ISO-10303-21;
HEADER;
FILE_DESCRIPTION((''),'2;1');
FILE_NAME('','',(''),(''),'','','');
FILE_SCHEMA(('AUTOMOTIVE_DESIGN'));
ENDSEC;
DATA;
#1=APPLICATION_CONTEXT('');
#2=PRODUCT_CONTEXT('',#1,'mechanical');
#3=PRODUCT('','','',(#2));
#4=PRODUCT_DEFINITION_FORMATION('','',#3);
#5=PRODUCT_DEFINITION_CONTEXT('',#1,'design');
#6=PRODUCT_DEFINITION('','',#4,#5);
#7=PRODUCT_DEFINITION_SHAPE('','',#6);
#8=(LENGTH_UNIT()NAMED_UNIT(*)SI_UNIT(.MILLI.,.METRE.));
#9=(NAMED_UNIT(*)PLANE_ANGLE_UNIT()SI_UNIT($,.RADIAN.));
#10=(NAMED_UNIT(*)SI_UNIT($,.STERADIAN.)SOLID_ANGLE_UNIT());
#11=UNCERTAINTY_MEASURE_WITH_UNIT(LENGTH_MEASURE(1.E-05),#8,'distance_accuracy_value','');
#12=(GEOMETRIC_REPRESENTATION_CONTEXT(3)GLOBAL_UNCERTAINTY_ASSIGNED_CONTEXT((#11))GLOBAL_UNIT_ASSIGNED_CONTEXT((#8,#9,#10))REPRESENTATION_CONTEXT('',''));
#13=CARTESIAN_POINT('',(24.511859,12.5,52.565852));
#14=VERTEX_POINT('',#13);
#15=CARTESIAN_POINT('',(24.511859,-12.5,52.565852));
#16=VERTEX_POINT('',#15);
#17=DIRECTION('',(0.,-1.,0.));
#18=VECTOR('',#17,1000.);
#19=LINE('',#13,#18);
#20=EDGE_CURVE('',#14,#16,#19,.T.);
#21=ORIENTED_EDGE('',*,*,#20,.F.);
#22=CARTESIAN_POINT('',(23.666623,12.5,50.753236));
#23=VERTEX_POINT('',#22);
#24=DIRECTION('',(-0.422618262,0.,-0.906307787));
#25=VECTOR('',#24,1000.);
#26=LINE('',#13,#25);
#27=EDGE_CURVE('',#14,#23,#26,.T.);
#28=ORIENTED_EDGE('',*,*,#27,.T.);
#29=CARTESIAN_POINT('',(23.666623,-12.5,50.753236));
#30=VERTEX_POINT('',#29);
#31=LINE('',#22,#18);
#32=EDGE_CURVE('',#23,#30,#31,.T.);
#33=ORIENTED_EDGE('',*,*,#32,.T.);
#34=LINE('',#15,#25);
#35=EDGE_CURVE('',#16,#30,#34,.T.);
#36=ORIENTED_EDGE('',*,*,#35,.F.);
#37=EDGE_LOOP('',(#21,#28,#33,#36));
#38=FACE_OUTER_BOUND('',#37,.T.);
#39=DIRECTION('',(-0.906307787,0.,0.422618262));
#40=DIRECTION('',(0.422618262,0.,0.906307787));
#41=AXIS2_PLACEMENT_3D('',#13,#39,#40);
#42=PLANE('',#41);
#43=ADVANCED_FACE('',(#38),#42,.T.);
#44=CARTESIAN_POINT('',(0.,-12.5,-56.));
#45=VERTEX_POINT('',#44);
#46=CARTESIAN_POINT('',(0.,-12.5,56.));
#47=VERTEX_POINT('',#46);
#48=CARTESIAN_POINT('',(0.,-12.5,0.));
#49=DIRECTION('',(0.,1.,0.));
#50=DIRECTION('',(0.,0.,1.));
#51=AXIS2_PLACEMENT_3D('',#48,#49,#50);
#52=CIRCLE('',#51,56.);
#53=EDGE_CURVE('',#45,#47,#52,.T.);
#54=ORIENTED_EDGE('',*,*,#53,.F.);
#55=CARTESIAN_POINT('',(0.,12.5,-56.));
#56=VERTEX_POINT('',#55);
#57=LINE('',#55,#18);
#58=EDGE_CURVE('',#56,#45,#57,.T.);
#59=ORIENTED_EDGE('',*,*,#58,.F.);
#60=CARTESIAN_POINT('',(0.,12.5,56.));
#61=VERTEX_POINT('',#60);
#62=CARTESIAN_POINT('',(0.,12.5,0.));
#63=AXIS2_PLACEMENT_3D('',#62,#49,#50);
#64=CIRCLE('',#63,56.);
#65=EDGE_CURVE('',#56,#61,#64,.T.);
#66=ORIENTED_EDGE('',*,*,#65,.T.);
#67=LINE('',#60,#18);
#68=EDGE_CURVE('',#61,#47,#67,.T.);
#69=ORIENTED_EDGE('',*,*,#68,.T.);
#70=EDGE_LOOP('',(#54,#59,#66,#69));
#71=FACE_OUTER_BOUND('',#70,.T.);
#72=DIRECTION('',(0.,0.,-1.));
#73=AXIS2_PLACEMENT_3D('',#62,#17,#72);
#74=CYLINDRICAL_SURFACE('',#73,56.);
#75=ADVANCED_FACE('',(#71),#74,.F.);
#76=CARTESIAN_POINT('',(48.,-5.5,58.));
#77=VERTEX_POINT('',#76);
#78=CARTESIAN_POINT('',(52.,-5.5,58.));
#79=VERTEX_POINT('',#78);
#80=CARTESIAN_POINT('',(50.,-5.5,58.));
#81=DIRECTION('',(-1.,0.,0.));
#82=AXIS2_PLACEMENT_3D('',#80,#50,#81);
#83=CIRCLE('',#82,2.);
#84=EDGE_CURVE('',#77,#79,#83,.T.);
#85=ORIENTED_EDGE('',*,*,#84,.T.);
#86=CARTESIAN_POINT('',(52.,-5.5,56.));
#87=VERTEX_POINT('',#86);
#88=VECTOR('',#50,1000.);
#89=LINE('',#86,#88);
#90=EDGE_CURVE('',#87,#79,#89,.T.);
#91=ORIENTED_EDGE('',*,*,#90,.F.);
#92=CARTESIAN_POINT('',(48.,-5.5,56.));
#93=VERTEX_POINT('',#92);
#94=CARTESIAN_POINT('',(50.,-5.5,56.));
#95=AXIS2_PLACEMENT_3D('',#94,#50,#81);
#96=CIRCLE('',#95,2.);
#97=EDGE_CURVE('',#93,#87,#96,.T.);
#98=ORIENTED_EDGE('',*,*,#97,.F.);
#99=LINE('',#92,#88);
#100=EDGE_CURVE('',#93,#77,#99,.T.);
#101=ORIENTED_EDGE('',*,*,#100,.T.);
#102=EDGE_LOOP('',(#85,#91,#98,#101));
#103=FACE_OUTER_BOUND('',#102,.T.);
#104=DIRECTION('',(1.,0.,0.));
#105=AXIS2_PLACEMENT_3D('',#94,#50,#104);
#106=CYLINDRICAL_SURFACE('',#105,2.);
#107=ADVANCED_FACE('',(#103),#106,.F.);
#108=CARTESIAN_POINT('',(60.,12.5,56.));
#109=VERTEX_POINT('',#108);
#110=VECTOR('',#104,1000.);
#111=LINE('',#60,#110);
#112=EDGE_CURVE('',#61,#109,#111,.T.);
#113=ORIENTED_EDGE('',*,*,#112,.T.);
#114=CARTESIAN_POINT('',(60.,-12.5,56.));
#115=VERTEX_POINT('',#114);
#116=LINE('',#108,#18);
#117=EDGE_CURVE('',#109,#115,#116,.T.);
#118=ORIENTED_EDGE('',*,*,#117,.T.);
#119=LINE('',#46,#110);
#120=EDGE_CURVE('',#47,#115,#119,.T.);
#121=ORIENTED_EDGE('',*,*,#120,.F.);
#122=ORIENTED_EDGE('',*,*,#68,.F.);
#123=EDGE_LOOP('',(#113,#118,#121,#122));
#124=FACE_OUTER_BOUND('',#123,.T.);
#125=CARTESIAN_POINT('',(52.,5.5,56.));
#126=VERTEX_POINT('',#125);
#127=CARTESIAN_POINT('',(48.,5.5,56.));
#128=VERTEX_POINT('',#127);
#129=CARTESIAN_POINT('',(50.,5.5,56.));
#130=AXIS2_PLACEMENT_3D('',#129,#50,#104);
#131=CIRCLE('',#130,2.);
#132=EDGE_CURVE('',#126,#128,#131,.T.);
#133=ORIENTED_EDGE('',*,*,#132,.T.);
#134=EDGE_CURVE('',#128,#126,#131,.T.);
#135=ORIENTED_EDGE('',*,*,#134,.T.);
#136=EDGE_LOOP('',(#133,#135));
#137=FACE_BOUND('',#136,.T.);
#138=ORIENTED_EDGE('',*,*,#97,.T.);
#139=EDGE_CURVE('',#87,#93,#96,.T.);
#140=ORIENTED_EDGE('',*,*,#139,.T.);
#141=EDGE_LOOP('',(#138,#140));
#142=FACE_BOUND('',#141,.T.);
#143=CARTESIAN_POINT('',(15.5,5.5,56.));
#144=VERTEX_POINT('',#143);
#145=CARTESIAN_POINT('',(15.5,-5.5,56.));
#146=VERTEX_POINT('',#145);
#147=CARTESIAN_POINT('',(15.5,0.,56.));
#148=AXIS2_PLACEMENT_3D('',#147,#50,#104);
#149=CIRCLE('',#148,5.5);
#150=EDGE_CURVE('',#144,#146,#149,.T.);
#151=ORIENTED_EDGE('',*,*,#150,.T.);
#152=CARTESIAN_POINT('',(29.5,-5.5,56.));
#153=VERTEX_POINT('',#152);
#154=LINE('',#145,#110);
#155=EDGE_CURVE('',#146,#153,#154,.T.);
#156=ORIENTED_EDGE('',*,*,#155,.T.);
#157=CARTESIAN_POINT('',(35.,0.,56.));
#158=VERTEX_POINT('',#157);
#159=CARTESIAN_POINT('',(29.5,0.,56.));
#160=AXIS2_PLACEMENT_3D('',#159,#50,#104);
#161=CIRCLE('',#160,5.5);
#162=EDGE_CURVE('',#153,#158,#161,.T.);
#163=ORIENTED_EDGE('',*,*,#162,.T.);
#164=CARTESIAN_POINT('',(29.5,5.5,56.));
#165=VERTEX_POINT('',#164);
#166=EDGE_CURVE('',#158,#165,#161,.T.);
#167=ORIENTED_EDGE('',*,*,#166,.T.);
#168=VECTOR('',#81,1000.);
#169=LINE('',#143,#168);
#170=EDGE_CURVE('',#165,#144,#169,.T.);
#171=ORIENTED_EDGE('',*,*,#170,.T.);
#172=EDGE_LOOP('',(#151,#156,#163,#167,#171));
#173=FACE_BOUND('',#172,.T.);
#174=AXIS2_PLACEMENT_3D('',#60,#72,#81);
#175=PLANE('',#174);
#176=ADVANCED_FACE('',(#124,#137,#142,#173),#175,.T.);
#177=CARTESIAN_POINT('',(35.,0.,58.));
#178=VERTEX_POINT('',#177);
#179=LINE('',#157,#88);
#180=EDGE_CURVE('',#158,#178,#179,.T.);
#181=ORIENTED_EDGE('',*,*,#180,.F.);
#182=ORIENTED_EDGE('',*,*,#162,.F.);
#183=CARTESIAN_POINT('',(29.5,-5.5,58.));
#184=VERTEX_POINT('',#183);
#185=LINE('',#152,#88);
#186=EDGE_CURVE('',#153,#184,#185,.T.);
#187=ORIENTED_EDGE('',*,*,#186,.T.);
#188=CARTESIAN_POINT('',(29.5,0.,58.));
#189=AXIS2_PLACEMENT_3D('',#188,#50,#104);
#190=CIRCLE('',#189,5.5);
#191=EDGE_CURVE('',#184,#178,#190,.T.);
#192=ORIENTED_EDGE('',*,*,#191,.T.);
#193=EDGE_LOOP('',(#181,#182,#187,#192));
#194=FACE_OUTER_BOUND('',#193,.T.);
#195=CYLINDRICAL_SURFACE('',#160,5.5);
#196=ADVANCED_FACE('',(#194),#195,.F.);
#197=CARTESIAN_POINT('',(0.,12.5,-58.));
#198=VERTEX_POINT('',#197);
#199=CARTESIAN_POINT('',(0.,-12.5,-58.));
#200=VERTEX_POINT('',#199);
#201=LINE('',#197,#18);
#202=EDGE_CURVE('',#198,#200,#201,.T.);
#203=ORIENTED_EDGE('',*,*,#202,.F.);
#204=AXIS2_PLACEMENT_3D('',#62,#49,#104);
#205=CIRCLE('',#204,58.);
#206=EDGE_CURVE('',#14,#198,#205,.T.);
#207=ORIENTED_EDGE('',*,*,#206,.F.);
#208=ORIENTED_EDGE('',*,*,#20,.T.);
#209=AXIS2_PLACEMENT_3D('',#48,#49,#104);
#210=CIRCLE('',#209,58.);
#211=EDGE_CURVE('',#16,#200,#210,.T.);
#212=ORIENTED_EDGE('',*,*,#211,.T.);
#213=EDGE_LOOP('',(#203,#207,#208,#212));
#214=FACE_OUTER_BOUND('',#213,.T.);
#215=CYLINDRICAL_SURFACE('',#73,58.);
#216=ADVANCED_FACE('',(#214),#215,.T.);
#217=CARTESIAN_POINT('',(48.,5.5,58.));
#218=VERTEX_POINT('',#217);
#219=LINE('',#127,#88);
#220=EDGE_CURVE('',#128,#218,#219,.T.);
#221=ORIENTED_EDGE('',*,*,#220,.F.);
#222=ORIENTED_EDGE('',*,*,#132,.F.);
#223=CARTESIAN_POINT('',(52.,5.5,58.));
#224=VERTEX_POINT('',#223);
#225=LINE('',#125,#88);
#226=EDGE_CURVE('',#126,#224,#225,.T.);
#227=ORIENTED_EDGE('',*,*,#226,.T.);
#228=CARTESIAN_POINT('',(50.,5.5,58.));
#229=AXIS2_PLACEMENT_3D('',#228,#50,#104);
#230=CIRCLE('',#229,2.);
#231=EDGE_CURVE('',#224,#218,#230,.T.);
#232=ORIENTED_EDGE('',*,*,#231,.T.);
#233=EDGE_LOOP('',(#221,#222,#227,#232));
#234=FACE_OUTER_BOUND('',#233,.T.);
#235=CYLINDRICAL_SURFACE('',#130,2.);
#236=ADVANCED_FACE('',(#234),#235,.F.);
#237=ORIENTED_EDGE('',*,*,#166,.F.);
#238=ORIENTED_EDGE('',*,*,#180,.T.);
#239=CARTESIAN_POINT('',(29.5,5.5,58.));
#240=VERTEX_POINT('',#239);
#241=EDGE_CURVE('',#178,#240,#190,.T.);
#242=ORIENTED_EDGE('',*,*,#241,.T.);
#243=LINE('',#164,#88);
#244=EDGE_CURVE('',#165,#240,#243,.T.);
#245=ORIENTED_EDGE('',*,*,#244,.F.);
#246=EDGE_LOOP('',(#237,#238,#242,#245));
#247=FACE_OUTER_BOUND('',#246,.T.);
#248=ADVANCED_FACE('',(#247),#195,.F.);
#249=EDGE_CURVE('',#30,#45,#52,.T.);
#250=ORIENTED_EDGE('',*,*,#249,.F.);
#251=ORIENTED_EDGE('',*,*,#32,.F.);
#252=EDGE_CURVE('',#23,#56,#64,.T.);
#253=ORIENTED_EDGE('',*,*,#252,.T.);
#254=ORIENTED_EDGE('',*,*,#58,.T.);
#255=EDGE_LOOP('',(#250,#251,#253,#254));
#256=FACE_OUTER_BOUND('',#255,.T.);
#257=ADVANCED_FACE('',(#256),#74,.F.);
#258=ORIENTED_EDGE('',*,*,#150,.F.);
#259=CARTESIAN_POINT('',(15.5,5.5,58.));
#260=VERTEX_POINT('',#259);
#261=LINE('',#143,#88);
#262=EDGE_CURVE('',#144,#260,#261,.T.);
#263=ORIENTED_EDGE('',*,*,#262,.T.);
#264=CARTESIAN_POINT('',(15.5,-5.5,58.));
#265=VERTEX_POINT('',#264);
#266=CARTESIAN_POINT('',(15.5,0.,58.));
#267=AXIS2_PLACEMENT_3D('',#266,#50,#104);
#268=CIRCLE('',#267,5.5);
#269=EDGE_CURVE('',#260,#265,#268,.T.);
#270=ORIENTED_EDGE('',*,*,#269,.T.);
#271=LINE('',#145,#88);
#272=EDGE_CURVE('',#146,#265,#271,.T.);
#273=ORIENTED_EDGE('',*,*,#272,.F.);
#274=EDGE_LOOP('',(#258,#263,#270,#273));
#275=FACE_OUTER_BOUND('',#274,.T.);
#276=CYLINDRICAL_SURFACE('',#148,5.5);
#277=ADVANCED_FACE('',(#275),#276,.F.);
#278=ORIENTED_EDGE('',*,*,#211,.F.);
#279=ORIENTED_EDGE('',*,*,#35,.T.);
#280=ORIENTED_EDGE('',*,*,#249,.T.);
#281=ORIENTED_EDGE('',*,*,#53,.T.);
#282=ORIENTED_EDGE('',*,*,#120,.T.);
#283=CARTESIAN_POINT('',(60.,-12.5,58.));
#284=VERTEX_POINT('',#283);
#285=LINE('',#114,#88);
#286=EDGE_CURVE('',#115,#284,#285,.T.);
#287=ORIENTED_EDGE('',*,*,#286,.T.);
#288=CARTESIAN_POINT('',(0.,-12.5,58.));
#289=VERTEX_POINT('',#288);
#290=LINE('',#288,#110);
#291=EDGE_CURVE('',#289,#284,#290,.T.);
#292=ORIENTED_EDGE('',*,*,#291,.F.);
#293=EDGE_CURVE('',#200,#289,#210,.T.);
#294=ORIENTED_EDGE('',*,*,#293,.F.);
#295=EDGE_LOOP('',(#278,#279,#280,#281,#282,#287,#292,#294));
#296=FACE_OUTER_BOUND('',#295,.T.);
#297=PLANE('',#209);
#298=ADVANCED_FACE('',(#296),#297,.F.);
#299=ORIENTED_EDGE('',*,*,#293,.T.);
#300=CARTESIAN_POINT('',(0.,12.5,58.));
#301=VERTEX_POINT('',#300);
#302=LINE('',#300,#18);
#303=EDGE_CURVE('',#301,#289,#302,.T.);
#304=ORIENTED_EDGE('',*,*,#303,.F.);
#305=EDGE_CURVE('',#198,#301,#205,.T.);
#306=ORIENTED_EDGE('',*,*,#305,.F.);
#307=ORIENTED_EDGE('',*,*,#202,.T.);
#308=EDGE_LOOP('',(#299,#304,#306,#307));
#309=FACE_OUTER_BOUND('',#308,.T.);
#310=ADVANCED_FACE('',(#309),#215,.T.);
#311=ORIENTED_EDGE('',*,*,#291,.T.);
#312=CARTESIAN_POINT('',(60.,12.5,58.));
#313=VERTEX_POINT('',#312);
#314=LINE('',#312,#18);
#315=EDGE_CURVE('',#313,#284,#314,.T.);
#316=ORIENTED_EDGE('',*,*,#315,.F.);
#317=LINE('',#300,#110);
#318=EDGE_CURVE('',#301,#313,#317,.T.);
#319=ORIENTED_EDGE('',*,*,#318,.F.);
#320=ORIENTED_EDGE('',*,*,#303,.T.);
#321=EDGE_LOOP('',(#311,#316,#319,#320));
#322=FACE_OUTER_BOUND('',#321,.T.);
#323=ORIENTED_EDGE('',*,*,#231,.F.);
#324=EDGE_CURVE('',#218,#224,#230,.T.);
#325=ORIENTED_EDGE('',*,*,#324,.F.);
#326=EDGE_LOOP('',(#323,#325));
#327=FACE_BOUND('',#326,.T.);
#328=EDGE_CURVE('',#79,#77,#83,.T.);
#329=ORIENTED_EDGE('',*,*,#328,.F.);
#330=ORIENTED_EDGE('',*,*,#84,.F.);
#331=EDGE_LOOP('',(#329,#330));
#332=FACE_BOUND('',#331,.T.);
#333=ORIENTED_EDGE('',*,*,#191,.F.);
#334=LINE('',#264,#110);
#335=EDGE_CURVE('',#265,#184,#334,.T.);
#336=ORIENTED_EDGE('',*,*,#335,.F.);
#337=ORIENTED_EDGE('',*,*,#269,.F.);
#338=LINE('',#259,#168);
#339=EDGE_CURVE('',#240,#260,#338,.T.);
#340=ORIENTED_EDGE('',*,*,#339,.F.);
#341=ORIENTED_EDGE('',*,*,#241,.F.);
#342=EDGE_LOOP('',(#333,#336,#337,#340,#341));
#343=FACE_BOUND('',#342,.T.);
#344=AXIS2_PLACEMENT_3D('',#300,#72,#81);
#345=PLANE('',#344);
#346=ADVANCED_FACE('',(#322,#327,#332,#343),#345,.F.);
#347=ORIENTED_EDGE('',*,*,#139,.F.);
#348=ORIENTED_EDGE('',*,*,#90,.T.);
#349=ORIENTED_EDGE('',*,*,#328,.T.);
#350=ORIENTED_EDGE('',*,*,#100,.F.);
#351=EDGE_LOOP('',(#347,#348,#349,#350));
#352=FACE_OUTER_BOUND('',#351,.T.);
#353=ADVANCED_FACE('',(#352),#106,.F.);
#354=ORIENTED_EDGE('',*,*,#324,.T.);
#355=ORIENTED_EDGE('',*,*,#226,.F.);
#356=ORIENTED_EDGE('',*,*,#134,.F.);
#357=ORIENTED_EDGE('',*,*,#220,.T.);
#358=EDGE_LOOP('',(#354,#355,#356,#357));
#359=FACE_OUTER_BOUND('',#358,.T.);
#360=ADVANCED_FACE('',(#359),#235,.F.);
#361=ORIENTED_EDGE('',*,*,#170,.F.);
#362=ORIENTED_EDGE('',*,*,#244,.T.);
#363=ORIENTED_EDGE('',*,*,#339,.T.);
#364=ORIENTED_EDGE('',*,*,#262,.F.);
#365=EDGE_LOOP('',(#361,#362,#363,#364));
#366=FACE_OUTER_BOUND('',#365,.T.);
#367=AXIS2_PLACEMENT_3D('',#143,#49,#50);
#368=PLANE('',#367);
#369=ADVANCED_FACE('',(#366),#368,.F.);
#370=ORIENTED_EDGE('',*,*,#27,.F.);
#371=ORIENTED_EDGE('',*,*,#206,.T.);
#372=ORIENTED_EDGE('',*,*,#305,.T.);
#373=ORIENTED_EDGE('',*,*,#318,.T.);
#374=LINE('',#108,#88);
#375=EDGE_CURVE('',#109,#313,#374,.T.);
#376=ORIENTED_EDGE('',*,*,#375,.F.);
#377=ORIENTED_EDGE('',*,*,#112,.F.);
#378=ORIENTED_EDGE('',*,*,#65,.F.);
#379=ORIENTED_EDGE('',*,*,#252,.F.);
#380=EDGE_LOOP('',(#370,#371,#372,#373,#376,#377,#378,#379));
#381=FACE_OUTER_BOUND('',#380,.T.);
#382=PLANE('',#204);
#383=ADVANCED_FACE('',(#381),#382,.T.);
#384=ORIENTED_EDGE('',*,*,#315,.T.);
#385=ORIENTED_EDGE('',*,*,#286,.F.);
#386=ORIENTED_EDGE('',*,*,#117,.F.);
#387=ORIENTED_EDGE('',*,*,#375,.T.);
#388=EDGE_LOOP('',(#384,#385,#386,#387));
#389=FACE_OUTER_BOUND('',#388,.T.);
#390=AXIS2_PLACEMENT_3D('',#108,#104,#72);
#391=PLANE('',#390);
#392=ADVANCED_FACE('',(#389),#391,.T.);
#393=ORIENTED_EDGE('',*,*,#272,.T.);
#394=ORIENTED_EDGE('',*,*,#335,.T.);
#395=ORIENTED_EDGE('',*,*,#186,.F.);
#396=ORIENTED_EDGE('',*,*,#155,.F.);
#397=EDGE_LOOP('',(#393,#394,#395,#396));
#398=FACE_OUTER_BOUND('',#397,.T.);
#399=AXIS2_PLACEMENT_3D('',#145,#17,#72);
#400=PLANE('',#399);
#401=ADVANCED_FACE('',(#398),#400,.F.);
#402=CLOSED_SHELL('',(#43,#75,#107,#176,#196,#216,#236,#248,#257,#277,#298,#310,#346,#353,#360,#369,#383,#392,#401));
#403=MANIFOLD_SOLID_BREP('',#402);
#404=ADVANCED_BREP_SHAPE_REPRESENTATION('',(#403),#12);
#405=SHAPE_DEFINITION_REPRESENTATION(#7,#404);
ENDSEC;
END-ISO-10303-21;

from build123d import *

# Parameters (mm, degrees)
EXTRUDE_1_DEPTH     = 12.5
SKETCH_3_R          = 2
CUT_EXTRUDE_1_DEPTH = 2


with BuildPart() as part:
    # 草图1 → 拉伸-薄壁1 (new, symmetric)
    with BuildSketch(Plane(origin=(0, 0, 0), x_dir=(1, 0, 0), z_dir=(0, 1, 0))):
        with BuildLine():
            ThreePointArc((23.666622657, -50.753236074), (-12.120618381, 54.672576399), (0, -56))
            Line((0, -56), (60, -56))
            Line((60, -56), (60, -58))
            Line((60, -58), (0, -58))
            ThreePointArc((0, -58), (-12.553497608, 56.625168413), (24.511859181, -52.565851648))
            Line((24.511859181, -52.565851648), (23.666622657, -50.753236074))
        make_face()
    extrude(amount=EXTRUDE_1_DEPTH, both=True)

    # 草图3 → 切除-拉伸1 (cut)
    with BuildSketch(Plane.XY.offset(58)):
        with Locations((50, 5.5)):
            Circle(SKETCH_3_R)
        with Locations(Location((50, -5.5, 0), (0, 0, 180))):
            Circle(SKETCH_3_R)
        with BuildLine():
            Line((15.5, 5.5), (29.5, 5.5))
            ThreePointArc((29.5, 5.5), (35, 0), (29.5, -5.5))
            Line((29.5, -5.5), (15.5, -5.5))
            ThreePointArc((15.5, -5.5), (10, 0), (15.5, 5.5))
        make_face()
    extrude(amount=-CUT_EXTRUDE_1_DEPTH, mode=Mode.SUBTRACT)


solid = part.part
